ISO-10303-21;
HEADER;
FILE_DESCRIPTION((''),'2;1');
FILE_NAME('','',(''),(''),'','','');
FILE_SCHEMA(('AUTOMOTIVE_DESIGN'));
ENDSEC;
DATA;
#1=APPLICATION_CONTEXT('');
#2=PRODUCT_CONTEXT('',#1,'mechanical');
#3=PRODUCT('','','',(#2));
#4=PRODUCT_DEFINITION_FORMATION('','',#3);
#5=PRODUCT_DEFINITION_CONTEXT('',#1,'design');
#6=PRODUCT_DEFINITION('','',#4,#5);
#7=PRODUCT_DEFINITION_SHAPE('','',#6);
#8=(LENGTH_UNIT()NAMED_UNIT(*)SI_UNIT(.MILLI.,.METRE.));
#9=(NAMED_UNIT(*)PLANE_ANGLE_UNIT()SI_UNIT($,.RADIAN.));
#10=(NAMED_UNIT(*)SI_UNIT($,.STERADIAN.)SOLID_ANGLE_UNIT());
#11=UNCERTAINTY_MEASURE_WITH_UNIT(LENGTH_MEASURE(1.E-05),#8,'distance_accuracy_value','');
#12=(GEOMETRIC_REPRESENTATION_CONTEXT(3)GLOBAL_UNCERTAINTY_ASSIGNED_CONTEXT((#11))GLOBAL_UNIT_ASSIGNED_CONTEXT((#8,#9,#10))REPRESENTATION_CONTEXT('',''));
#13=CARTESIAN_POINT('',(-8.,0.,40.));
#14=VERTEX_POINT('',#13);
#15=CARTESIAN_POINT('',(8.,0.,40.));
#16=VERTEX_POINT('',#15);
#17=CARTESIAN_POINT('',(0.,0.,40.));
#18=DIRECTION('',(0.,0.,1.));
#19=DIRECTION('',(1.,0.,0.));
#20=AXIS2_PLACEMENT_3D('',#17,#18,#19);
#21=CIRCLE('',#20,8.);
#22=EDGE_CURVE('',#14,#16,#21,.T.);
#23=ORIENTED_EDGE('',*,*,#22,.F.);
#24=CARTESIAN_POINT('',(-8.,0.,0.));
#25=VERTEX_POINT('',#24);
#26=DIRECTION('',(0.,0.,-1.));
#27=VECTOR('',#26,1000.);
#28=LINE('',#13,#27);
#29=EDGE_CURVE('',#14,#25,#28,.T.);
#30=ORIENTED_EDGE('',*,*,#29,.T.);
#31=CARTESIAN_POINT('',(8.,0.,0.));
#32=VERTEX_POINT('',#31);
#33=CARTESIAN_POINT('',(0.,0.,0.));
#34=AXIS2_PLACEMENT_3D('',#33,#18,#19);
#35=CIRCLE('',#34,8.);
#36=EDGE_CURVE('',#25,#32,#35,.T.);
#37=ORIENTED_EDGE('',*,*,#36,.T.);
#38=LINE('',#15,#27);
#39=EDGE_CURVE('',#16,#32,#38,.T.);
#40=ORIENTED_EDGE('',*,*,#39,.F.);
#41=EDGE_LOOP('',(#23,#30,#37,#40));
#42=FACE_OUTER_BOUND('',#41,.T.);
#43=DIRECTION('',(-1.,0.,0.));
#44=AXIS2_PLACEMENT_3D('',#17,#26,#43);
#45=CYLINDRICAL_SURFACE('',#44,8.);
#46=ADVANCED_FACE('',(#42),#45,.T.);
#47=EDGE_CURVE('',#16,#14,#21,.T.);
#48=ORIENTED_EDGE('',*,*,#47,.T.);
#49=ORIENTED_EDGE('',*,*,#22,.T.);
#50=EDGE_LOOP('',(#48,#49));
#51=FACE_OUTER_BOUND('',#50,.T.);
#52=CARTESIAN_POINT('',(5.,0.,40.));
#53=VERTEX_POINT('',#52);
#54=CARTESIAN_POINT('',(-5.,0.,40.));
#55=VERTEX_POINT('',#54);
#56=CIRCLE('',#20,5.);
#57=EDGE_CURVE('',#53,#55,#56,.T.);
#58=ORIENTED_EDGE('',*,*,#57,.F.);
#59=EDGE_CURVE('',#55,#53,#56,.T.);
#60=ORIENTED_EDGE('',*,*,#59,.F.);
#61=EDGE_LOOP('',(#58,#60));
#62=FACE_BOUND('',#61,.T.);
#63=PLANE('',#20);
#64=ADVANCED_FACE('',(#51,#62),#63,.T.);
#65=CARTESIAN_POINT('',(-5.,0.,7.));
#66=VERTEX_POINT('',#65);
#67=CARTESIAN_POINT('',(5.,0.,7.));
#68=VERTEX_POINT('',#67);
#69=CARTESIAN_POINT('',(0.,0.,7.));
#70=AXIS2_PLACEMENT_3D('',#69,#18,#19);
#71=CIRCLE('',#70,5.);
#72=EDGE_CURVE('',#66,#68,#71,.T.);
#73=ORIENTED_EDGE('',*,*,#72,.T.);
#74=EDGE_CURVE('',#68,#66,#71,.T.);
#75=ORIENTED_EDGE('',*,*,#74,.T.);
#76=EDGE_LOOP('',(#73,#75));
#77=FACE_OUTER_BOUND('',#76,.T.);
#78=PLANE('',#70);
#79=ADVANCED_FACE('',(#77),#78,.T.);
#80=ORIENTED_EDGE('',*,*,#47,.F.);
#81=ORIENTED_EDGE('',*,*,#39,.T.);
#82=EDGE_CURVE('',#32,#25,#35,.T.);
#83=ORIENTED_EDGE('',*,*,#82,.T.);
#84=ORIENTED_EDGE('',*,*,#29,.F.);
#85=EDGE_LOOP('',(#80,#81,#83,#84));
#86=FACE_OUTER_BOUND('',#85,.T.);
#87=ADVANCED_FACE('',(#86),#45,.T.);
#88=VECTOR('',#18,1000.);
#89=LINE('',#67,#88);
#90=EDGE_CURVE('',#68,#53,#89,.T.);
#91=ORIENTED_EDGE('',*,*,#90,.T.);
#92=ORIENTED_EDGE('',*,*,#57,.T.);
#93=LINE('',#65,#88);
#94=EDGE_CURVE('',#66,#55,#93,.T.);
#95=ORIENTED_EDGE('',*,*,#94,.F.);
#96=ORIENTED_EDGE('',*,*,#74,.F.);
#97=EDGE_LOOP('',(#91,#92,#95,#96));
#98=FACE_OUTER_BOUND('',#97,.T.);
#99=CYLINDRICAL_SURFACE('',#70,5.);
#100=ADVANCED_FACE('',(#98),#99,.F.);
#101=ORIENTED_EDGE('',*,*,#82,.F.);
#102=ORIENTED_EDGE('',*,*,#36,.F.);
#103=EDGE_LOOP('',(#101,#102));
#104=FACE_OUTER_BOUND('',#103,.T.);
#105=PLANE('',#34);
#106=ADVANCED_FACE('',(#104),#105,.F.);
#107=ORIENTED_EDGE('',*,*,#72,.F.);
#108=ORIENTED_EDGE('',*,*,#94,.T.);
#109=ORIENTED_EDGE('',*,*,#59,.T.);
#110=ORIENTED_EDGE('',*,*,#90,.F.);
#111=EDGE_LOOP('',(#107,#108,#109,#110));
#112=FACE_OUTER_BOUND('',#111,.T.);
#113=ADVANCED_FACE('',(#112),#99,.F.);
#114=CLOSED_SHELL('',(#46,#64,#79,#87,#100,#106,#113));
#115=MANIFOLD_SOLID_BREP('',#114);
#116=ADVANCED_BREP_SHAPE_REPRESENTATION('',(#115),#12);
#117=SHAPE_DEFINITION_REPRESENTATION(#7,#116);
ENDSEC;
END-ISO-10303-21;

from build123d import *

# Parameters (mm, degrees)
SKETCH1_R           = 8
BOSS_EXTRUDE1_DEPTH = 40
SKETCH2_R           = 5
CUT_EXTRUDE1_DEPTH  = 33


with BuildPart() as part:
    # Sketch1 → Boss-Extrude1 (new body)
    with BuildSketch(Plane.XY):
        Circle(SKETCH1_R)
    extrude(amount=BOSS_EXTRUDE1_DEPTH)

    # Sketch2 → Cut-Extrude1 (cut)
    with BuildSketch(Plane.XY.offset(40)):
        Circle(SKETCH2_R)
    extrude(amount=-CUT_EXTRUDE1_DEPTH, mode=Mode.SUBTRACT)


solid = part.part
